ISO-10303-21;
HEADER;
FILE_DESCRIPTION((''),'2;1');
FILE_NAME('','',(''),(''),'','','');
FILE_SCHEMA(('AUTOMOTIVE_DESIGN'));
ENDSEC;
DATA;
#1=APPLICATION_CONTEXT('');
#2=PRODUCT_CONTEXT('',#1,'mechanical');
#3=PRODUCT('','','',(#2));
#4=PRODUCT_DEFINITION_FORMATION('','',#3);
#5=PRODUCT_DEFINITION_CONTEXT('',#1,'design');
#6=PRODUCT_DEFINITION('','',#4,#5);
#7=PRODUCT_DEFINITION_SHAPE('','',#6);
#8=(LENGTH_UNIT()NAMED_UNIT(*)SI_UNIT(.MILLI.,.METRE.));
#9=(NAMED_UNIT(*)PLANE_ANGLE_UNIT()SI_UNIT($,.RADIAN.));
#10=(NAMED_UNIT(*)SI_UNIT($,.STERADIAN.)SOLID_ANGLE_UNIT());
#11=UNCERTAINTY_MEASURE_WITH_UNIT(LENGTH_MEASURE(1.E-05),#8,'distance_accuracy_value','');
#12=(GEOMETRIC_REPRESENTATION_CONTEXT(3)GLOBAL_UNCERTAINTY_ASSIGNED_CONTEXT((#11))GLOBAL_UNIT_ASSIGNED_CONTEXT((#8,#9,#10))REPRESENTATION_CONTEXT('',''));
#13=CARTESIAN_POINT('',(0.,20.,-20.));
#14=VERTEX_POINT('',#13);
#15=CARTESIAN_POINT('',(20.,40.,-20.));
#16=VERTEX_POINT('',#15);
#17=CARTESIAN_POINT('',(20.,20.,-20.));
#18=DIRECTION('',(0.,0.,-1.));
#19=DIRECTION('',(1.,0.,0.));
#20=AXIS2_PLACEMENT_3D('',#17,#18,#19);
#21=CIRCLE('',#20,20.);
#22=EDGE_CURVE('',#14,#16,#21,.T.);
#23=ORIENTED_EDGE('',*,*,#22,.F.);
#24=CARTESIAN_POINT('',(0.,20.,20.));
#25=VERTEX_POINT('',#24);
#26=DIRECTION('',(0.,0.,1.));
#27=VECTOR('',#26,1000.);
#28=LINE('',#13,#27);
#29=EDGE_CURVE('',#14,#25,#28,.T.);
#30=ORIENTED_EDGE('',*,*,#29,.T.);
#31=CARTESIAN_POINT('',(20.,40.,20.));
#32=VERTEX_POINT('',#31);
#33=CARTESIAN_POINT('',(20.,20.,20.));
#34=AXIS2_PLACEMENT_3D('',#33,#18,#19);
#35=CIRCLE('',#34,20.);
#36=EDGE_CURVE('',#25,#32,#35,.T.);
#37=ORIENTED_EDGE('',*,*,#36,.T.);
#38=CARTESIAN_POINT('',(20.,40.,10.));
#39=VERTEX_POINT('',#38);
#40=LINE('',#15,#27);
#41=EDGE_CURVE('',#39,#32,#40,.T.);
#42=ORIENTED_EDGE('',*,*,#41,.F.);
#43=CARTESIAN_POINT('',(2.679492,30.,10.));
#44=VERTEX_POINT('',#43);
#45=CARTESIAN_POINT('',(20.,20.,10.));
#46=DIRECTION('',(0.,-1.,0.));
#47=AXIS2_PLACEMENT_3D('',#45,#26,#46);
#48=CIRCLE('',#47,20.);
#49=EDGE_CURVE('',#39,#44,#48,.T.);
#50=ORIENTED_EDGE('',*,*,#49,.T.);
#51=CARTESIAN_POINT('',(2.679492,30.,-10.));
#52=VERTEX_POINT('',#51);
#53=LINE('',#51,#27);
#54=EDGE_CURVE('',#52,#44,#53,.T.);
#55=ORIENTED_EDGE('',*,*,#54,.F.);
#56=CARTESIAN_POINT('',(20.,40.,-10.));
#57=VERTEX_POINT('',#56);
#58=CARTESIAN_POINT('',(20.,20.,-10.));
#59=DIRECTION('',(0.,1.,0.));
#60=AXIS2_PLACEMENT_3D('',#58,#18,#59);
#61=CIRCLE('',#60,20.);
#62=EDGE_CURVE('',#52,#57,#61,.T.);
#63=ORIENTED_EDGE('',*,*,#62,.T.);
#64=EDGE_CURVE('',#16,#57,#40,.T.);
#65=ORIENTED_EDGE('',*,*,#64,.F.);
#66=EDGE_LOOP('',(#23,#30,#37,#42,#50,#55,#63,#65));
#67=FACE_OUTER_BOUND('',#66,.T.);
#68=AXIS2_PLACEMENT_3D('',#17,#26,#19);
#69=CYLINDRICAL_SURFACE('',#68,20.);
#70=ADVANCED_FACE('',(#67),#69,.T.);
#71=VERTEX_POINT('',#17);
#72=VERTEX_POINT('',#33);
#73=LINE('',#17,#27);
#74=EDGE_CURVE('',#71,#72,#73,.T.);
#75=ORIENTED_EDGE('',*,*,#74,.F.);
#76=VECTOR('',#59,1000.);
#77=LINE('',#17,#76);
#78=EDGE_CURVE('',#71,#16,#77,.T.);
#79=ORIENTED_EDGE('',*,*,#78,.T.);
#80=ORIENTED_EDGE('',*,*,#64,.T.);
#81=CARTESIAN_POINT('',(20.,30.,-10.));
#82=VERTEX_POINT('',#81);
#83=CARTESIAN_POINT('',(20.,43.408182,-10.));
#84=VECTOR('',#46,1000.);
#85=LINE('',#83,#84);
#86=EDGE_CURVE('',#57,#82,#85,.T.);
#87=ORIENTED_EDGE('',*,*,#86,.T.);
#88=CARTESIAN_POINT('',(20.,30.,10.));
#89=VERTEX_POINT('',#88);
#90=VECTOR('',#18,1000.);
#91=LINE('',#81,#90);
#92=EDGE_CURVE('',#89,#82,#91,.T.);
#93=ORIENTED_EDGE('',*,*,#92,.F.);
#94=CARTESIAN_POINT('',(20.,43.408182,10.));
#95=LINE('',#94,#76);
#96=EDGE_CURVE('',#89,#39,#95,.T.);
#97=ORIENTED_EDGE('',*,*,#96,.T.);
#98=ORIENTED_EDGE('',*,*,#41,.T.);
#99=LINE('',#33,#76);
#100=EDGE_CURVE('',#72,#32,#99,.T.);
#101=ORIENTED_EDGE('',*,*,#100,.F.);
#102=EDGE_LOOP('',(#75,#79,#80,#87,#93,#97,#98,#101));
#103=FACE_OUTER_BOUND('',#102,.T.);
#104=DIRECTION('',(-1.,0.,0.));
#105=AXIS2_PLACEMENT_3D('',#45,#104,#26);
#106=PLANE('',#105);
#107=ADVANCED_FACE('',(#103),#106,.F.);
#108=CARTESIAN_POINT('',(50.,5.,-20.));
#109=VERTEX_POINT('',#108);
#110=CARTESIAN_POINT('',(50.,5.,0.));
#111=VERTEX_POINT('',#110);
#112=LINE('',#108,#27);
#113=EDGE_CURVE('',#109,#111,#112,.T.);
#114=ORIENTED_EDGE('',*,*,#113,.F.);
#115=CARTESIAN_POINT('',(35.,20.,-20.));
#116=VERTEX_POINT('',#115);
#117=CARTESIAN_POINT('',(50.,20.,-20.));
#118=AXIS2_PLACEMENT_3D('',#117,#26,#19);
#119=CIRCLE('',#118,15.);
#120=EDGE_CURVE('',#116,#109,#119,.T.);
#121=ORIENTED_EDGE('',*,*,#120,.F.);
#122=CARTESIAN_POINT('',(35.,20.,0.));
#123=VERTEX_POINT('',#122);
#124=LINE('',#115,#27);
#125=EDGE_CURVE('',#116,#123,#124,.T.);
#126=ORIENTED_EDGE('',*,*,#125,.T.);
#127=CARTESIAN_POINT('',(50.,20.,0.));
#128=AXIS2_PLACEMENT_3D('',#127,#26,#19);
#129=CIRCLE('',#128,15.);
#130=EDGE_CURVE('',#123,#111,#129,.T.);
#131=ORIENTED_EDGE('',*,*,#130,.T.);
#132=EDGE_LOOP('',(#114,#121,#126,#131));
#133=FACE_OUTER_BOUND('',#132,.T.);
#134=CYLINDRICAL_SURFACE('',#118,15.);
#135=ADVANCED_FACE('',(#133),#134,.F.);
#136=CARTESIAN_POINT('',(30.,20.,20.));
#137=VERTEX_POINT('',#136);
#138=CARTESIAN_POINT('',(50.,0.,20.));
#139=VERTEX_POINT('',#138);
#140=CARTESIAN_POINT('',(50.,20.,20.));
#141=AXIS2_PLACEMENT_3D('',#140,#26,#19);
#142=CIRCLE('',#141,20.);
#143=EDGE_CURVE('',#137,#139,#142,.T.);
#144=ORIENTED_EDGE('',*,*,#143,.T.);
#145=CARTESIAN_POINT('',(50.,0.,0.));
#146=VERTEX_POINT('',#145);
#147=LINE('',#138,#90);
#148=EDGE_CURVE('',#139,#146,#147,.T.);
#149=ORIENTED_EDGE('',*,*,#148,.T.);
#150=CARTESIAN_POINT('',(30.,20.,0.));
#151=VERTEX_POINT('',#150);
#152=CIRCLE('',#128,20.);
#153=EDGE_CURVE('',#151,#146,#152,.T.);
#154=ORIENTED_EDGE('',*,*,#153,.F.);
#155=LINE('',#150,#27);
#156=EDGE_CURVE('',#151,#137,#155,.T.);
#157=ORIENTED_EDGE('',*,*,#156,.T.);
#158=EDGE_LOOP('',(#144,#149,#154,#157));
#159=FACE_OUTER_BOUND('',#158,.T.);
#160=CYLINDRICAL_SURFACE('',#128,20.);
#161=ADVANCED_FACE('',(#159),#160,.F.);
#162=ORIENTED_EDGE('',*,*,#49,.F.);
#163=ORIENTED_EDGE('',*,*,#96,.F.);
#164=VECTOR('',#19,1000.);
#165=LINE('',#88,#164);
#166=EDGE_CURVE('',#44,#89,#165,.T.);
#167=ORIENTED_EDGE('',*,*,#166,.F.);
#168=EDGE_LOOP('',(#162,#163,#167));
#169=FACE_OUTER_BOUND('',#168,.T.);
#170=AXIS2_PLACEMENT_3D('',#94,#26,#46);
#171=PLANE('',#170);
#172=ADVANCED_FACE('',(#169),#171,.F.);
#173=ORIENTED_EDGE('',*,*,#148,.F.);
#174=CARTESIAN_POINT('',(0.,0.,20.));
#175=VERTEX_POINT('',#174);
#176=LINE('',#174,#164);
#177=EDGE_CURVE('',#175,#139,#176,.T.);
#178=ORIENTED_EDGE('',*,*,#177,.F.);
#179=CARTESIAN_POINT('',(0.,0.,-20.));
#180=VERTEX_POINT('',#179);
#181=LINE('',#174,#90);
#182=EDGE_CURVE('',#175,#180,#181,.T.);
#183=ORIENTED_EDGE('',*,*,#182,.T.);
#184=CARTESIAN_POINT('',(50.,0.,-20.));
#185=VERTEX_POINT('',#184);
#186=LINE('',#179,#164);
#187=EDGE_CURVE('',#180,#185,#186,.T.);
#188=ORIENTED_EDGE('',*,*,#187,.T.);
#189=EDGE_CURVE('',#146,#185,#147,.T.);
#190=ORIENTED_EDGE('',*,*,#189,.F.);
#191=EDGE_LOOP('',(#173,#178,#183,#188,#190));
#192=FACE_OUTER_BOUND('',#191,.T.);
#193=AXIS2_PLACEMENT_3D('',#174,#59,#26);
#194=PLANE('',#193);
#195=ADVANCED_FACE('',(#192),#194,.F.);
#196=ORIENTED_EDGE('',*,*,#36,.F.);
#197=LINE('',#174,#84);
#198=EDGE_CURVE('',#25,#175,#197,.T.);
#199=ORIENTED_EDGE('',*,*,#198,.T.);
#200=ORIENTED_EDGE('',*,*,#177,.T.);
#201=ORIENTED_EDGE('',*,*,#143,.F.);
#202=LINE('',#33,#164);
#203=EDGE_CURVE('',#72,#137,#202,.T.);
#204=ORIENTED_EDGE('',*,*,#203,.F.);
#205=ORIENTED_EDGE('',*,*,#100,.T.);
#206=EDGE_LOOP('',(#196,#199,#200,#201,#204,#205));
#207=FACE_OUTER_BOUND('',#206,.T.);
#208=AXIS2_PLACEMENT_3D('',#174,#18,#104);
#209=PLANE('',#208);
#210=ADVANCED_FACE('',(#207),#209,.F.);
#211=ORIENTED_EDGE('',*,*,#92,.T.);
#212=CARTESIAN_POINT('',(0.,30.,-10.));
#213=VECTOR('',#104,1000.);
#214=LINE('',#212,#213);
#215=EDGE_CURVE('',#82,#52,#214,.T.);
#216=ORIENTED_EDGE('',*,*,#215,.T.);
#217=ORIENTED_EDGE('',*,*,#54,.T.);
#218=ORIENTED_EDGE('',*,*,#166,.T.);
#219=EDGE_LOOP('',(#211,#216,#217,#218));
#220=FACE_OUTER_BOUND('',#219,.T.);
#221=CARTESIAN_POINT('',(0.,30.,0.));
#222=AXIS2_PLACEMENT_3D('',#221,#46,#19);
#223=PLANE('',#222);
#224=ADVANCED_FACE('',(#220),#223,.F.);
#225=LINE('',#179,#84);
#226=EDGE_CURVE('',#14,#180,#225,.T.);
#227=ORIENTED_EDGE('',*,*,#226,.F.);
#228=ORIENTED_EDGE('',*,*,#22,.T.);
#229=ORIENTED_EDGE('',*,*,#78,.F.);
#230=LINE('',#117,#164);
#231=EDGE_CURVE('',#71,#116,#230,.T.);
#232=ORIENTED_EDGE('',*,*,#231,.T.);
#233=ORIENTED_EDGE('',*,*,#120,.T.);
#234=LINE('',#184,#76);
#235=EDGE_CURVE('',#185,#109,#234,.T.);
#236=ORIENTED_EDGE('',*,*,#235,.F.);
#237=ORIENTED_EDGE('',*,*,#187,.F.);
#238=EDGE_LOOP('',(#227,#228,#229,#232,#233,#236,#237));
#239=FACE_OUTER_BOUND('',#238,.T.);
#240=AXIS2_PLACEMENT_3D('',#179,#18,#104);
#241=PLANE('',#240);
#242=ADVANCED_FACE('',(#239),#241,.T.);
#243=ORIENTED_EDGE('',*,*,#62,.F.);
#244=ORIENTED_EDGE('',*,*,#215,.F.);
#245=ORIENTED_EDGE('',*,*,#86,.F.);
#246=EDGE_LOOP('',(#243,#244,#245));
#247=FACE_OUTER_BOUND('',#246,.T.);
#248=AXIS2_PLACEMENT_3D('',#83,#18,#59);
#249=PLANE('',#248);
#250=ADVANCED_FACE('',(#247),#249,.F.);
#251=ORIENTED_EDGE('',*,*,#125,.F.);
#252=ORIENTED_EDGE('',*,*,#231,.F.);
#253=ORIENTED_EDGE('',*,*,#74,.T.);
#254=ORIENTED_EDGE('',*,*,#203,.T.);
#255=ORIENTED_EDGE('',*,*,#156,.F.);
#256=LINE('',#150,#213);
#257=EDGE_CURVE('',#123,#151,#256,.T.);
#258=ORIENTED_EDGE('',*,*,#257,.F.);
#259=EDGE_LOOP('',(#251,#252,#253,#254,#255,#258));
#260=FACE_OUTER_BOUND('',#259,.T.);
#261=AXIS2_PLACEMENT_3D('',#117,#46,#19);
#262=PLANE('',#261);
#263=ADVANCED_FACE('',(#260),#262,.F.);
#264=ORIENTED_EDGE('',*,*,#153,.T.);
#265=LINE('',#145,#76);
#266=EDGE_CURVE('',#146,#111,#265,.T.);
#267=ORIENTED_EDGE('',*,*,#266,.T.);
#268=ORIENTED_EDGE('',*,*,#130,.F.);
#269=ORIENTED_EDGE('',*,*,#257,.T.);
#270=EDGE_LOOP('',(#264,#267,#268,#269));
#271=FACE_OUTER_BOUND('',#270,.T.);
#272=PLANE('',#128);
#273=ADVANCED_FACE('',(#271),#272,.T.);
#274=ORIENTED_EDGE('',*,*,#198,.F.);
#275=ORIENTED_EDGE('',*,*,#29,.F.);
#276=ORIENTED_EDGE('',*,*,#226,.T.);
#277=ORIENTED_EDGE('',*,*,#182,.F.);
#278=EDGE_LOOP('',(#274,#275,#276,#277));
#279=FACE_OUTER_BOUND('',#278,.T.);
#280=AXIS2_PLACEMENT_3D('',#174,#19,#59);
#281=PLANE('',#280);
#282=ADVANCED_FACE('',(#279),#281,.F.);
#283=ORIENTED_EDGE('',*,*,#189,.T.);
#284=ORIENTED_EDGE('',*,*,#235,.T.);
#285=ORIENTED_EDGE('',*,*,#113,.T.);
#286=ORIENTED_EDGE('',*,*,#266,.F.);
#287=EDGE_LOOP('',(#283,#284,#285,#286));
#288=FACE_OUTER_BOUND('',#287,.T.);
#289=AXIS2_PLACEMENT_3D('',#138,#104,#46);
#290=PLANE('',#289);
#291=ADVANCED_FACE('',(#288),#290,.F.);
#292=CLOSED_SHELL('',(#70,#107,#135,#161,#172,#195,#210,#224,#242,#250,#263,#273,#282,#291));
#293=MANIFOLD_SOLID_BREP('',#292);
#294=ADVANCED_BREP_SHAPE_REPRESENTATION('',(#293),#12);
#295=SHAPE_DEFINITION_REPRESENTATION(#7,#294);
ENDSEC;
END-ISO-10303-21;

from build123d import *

# Parameters (mm, degrees)
BASE_BLOCK_PROFILE_W      = 50
BASE_BLOCK_PROFILE_H      = 40
BASE_BLOCK_50X40X40_DEPTH = 20
CORNER_NOTCH_PROFILE_W    = 20
CORNER_NOTCH_PROFILE_H    = 20
CORNER_NOTCH_20X20_DEPTH  = 76.498344353
STEP_CUT_DEPTH            = 20
CONCAVE_ARC_CUT_DEPTH     = 20
ARC_GROOVE_CUT_DEPTH      = 76.498344353
TOP_SLOT_PROFILE_10X10_W  = 20
TOP_SLOT_PROFILE_10X10_H  = 23.40818189
TOP_SLOT_10X10_DEPTH      = 20
ROUNDED_TOP_CUT_DEPTH     = 20
RIDGE_BOSS_PROFILE_W      = 20
RIDGE_BOSS_PROFILE_H      = 20
RIDGE_BOSS_10_DEPTH       = 10
RIDGE_ROUND_CUT_DEPTH     = 20


with BuildPart() as part:
    # Base Block Profile → Base Block 50x40x40 (new, symmetric)
    with BuildSketch(Plane.XY):
        with Locations((25, 20)):
            Rectangle(BASE_BLOCK_PROFILE_W, BASE_BLOCK_PROFILE_H)
    extrude(amount=BASE_BLOCK_50X40X40_DEPTH, both=True)

    # Corner Notch Profile → Corner Notch 20x20 (cut, through all)
    with BuildSketch(Plane.XY.offset(20)):
        with Locations((40, 30)):
            Rectangle(CORNER_NOTCH_PROFILE_W, CORNER_NOTCH_PROFILE_H)
    extrude(amount=-CORNER_NOTCH_20X20_DEPTH, mode=Mode.SUBTRACT)

    # Step Cut Profile → Step Cut (cut)
    with BuildSketch(Plane.XY.offset(20)):
        with BuildLine():
            Line((50, 0), (50, 20))
            Line((50, 20), (30, 20))
            ThreePointArc((30, 20), (35.857864376, 5.857864376), (50, 0))
        make_face()
    extrude(amount=-STEP_CUT_DEPTH, mode=Mode.SUBTRACT)

    # Concave Arc Profile R30 → Concave Arc Cut (cut)
    with BuildSketch(Plane.XY):
        with BuildLine():
            Line((50, 5), (50, 20))
            Line((50, 20), (35, 20))
            ThreePointArc((35, 20), (39.393398282, 9.393398282), (50, 5))
        make_face()
    extrude(amount=-CONCAVE_ARC_CUT_DEPTH, mode=Mode.SUBTRACT)

    # Arc Groove Profile → Arc Groove Cut (cut, through all)
    with BuildSketch(Plane.XY.offset(20)):
        with BuildLine():
            Line((0, 40), (0, 20))
            ThreePointArc((0, 20), (5.857864376, 34.142135624), (20, 40))
            Line((20, 40), (0, 40))
        make_face()
    extrude(amount=-ARC_GROOVE_CUT_DEPTH, mode=Mode.SUBTRACT)

    # Top Slot Profile 10x10 → Top Slot 10x10 (cut)
    with BuildSketch(Plane.ZY):
        with Locations((0, 31.704090945)):
            Rectangle(TOP_SLOT_PROFILE_10X10_W, TOP_SLOT_PROFILE_10X10_H)
    extrude(amount=-TOP_SLOT_10X10_DEPTH, mode=Mode.SUBTRACT)

    # Rounded Top Profile → Rounded Top Cut (cut)
    with BuildSketch(Plane(origin=(0, 40, 0), x_dir=(1, 0, 0), z_dir=(0, 1, 0))):
        Polygon((20, 20), (20, 10), (20, -10), (20, -20), (30, -20), (30, 20), align=None)
    extrude(amount=-ROUNDED_TOP_CUT_DEPTH, mode=Mode.SUBTRACT)

    # Ridge Boss Profile → Ridge Boss 10 (add)
    with BuildSketch(Plane(origin=(0, 20, 0), x_dir=(1, 0, 0), z_dir=(0, 1, 0))):
        with Locations((10, 0)):
            Rectangle(RIDGE_BOSS_PROFILE_W, RIDGE_BOSS_PROFILE_H)
    extrude(amount=RIDGE_BOSS_10_DEPTH)

    # Ridge Round Profile → Ridge Round Cut (cut)
    with BuildSketch(Plane.XY.offset(10)):
        with BuildLine():
            Line((0, 30), (0, 20))
            ThreePointArc((0, 20), (0.681483474, 25.176380902), (2.679491924, 30))
            Line((2.679491924, 30), (0, 30))
        make_face()
    extrude(amount=-RIDGE_ROUND_CUT_DEPTH, mode=Mode.SUBTRACT)


solid = part.part
